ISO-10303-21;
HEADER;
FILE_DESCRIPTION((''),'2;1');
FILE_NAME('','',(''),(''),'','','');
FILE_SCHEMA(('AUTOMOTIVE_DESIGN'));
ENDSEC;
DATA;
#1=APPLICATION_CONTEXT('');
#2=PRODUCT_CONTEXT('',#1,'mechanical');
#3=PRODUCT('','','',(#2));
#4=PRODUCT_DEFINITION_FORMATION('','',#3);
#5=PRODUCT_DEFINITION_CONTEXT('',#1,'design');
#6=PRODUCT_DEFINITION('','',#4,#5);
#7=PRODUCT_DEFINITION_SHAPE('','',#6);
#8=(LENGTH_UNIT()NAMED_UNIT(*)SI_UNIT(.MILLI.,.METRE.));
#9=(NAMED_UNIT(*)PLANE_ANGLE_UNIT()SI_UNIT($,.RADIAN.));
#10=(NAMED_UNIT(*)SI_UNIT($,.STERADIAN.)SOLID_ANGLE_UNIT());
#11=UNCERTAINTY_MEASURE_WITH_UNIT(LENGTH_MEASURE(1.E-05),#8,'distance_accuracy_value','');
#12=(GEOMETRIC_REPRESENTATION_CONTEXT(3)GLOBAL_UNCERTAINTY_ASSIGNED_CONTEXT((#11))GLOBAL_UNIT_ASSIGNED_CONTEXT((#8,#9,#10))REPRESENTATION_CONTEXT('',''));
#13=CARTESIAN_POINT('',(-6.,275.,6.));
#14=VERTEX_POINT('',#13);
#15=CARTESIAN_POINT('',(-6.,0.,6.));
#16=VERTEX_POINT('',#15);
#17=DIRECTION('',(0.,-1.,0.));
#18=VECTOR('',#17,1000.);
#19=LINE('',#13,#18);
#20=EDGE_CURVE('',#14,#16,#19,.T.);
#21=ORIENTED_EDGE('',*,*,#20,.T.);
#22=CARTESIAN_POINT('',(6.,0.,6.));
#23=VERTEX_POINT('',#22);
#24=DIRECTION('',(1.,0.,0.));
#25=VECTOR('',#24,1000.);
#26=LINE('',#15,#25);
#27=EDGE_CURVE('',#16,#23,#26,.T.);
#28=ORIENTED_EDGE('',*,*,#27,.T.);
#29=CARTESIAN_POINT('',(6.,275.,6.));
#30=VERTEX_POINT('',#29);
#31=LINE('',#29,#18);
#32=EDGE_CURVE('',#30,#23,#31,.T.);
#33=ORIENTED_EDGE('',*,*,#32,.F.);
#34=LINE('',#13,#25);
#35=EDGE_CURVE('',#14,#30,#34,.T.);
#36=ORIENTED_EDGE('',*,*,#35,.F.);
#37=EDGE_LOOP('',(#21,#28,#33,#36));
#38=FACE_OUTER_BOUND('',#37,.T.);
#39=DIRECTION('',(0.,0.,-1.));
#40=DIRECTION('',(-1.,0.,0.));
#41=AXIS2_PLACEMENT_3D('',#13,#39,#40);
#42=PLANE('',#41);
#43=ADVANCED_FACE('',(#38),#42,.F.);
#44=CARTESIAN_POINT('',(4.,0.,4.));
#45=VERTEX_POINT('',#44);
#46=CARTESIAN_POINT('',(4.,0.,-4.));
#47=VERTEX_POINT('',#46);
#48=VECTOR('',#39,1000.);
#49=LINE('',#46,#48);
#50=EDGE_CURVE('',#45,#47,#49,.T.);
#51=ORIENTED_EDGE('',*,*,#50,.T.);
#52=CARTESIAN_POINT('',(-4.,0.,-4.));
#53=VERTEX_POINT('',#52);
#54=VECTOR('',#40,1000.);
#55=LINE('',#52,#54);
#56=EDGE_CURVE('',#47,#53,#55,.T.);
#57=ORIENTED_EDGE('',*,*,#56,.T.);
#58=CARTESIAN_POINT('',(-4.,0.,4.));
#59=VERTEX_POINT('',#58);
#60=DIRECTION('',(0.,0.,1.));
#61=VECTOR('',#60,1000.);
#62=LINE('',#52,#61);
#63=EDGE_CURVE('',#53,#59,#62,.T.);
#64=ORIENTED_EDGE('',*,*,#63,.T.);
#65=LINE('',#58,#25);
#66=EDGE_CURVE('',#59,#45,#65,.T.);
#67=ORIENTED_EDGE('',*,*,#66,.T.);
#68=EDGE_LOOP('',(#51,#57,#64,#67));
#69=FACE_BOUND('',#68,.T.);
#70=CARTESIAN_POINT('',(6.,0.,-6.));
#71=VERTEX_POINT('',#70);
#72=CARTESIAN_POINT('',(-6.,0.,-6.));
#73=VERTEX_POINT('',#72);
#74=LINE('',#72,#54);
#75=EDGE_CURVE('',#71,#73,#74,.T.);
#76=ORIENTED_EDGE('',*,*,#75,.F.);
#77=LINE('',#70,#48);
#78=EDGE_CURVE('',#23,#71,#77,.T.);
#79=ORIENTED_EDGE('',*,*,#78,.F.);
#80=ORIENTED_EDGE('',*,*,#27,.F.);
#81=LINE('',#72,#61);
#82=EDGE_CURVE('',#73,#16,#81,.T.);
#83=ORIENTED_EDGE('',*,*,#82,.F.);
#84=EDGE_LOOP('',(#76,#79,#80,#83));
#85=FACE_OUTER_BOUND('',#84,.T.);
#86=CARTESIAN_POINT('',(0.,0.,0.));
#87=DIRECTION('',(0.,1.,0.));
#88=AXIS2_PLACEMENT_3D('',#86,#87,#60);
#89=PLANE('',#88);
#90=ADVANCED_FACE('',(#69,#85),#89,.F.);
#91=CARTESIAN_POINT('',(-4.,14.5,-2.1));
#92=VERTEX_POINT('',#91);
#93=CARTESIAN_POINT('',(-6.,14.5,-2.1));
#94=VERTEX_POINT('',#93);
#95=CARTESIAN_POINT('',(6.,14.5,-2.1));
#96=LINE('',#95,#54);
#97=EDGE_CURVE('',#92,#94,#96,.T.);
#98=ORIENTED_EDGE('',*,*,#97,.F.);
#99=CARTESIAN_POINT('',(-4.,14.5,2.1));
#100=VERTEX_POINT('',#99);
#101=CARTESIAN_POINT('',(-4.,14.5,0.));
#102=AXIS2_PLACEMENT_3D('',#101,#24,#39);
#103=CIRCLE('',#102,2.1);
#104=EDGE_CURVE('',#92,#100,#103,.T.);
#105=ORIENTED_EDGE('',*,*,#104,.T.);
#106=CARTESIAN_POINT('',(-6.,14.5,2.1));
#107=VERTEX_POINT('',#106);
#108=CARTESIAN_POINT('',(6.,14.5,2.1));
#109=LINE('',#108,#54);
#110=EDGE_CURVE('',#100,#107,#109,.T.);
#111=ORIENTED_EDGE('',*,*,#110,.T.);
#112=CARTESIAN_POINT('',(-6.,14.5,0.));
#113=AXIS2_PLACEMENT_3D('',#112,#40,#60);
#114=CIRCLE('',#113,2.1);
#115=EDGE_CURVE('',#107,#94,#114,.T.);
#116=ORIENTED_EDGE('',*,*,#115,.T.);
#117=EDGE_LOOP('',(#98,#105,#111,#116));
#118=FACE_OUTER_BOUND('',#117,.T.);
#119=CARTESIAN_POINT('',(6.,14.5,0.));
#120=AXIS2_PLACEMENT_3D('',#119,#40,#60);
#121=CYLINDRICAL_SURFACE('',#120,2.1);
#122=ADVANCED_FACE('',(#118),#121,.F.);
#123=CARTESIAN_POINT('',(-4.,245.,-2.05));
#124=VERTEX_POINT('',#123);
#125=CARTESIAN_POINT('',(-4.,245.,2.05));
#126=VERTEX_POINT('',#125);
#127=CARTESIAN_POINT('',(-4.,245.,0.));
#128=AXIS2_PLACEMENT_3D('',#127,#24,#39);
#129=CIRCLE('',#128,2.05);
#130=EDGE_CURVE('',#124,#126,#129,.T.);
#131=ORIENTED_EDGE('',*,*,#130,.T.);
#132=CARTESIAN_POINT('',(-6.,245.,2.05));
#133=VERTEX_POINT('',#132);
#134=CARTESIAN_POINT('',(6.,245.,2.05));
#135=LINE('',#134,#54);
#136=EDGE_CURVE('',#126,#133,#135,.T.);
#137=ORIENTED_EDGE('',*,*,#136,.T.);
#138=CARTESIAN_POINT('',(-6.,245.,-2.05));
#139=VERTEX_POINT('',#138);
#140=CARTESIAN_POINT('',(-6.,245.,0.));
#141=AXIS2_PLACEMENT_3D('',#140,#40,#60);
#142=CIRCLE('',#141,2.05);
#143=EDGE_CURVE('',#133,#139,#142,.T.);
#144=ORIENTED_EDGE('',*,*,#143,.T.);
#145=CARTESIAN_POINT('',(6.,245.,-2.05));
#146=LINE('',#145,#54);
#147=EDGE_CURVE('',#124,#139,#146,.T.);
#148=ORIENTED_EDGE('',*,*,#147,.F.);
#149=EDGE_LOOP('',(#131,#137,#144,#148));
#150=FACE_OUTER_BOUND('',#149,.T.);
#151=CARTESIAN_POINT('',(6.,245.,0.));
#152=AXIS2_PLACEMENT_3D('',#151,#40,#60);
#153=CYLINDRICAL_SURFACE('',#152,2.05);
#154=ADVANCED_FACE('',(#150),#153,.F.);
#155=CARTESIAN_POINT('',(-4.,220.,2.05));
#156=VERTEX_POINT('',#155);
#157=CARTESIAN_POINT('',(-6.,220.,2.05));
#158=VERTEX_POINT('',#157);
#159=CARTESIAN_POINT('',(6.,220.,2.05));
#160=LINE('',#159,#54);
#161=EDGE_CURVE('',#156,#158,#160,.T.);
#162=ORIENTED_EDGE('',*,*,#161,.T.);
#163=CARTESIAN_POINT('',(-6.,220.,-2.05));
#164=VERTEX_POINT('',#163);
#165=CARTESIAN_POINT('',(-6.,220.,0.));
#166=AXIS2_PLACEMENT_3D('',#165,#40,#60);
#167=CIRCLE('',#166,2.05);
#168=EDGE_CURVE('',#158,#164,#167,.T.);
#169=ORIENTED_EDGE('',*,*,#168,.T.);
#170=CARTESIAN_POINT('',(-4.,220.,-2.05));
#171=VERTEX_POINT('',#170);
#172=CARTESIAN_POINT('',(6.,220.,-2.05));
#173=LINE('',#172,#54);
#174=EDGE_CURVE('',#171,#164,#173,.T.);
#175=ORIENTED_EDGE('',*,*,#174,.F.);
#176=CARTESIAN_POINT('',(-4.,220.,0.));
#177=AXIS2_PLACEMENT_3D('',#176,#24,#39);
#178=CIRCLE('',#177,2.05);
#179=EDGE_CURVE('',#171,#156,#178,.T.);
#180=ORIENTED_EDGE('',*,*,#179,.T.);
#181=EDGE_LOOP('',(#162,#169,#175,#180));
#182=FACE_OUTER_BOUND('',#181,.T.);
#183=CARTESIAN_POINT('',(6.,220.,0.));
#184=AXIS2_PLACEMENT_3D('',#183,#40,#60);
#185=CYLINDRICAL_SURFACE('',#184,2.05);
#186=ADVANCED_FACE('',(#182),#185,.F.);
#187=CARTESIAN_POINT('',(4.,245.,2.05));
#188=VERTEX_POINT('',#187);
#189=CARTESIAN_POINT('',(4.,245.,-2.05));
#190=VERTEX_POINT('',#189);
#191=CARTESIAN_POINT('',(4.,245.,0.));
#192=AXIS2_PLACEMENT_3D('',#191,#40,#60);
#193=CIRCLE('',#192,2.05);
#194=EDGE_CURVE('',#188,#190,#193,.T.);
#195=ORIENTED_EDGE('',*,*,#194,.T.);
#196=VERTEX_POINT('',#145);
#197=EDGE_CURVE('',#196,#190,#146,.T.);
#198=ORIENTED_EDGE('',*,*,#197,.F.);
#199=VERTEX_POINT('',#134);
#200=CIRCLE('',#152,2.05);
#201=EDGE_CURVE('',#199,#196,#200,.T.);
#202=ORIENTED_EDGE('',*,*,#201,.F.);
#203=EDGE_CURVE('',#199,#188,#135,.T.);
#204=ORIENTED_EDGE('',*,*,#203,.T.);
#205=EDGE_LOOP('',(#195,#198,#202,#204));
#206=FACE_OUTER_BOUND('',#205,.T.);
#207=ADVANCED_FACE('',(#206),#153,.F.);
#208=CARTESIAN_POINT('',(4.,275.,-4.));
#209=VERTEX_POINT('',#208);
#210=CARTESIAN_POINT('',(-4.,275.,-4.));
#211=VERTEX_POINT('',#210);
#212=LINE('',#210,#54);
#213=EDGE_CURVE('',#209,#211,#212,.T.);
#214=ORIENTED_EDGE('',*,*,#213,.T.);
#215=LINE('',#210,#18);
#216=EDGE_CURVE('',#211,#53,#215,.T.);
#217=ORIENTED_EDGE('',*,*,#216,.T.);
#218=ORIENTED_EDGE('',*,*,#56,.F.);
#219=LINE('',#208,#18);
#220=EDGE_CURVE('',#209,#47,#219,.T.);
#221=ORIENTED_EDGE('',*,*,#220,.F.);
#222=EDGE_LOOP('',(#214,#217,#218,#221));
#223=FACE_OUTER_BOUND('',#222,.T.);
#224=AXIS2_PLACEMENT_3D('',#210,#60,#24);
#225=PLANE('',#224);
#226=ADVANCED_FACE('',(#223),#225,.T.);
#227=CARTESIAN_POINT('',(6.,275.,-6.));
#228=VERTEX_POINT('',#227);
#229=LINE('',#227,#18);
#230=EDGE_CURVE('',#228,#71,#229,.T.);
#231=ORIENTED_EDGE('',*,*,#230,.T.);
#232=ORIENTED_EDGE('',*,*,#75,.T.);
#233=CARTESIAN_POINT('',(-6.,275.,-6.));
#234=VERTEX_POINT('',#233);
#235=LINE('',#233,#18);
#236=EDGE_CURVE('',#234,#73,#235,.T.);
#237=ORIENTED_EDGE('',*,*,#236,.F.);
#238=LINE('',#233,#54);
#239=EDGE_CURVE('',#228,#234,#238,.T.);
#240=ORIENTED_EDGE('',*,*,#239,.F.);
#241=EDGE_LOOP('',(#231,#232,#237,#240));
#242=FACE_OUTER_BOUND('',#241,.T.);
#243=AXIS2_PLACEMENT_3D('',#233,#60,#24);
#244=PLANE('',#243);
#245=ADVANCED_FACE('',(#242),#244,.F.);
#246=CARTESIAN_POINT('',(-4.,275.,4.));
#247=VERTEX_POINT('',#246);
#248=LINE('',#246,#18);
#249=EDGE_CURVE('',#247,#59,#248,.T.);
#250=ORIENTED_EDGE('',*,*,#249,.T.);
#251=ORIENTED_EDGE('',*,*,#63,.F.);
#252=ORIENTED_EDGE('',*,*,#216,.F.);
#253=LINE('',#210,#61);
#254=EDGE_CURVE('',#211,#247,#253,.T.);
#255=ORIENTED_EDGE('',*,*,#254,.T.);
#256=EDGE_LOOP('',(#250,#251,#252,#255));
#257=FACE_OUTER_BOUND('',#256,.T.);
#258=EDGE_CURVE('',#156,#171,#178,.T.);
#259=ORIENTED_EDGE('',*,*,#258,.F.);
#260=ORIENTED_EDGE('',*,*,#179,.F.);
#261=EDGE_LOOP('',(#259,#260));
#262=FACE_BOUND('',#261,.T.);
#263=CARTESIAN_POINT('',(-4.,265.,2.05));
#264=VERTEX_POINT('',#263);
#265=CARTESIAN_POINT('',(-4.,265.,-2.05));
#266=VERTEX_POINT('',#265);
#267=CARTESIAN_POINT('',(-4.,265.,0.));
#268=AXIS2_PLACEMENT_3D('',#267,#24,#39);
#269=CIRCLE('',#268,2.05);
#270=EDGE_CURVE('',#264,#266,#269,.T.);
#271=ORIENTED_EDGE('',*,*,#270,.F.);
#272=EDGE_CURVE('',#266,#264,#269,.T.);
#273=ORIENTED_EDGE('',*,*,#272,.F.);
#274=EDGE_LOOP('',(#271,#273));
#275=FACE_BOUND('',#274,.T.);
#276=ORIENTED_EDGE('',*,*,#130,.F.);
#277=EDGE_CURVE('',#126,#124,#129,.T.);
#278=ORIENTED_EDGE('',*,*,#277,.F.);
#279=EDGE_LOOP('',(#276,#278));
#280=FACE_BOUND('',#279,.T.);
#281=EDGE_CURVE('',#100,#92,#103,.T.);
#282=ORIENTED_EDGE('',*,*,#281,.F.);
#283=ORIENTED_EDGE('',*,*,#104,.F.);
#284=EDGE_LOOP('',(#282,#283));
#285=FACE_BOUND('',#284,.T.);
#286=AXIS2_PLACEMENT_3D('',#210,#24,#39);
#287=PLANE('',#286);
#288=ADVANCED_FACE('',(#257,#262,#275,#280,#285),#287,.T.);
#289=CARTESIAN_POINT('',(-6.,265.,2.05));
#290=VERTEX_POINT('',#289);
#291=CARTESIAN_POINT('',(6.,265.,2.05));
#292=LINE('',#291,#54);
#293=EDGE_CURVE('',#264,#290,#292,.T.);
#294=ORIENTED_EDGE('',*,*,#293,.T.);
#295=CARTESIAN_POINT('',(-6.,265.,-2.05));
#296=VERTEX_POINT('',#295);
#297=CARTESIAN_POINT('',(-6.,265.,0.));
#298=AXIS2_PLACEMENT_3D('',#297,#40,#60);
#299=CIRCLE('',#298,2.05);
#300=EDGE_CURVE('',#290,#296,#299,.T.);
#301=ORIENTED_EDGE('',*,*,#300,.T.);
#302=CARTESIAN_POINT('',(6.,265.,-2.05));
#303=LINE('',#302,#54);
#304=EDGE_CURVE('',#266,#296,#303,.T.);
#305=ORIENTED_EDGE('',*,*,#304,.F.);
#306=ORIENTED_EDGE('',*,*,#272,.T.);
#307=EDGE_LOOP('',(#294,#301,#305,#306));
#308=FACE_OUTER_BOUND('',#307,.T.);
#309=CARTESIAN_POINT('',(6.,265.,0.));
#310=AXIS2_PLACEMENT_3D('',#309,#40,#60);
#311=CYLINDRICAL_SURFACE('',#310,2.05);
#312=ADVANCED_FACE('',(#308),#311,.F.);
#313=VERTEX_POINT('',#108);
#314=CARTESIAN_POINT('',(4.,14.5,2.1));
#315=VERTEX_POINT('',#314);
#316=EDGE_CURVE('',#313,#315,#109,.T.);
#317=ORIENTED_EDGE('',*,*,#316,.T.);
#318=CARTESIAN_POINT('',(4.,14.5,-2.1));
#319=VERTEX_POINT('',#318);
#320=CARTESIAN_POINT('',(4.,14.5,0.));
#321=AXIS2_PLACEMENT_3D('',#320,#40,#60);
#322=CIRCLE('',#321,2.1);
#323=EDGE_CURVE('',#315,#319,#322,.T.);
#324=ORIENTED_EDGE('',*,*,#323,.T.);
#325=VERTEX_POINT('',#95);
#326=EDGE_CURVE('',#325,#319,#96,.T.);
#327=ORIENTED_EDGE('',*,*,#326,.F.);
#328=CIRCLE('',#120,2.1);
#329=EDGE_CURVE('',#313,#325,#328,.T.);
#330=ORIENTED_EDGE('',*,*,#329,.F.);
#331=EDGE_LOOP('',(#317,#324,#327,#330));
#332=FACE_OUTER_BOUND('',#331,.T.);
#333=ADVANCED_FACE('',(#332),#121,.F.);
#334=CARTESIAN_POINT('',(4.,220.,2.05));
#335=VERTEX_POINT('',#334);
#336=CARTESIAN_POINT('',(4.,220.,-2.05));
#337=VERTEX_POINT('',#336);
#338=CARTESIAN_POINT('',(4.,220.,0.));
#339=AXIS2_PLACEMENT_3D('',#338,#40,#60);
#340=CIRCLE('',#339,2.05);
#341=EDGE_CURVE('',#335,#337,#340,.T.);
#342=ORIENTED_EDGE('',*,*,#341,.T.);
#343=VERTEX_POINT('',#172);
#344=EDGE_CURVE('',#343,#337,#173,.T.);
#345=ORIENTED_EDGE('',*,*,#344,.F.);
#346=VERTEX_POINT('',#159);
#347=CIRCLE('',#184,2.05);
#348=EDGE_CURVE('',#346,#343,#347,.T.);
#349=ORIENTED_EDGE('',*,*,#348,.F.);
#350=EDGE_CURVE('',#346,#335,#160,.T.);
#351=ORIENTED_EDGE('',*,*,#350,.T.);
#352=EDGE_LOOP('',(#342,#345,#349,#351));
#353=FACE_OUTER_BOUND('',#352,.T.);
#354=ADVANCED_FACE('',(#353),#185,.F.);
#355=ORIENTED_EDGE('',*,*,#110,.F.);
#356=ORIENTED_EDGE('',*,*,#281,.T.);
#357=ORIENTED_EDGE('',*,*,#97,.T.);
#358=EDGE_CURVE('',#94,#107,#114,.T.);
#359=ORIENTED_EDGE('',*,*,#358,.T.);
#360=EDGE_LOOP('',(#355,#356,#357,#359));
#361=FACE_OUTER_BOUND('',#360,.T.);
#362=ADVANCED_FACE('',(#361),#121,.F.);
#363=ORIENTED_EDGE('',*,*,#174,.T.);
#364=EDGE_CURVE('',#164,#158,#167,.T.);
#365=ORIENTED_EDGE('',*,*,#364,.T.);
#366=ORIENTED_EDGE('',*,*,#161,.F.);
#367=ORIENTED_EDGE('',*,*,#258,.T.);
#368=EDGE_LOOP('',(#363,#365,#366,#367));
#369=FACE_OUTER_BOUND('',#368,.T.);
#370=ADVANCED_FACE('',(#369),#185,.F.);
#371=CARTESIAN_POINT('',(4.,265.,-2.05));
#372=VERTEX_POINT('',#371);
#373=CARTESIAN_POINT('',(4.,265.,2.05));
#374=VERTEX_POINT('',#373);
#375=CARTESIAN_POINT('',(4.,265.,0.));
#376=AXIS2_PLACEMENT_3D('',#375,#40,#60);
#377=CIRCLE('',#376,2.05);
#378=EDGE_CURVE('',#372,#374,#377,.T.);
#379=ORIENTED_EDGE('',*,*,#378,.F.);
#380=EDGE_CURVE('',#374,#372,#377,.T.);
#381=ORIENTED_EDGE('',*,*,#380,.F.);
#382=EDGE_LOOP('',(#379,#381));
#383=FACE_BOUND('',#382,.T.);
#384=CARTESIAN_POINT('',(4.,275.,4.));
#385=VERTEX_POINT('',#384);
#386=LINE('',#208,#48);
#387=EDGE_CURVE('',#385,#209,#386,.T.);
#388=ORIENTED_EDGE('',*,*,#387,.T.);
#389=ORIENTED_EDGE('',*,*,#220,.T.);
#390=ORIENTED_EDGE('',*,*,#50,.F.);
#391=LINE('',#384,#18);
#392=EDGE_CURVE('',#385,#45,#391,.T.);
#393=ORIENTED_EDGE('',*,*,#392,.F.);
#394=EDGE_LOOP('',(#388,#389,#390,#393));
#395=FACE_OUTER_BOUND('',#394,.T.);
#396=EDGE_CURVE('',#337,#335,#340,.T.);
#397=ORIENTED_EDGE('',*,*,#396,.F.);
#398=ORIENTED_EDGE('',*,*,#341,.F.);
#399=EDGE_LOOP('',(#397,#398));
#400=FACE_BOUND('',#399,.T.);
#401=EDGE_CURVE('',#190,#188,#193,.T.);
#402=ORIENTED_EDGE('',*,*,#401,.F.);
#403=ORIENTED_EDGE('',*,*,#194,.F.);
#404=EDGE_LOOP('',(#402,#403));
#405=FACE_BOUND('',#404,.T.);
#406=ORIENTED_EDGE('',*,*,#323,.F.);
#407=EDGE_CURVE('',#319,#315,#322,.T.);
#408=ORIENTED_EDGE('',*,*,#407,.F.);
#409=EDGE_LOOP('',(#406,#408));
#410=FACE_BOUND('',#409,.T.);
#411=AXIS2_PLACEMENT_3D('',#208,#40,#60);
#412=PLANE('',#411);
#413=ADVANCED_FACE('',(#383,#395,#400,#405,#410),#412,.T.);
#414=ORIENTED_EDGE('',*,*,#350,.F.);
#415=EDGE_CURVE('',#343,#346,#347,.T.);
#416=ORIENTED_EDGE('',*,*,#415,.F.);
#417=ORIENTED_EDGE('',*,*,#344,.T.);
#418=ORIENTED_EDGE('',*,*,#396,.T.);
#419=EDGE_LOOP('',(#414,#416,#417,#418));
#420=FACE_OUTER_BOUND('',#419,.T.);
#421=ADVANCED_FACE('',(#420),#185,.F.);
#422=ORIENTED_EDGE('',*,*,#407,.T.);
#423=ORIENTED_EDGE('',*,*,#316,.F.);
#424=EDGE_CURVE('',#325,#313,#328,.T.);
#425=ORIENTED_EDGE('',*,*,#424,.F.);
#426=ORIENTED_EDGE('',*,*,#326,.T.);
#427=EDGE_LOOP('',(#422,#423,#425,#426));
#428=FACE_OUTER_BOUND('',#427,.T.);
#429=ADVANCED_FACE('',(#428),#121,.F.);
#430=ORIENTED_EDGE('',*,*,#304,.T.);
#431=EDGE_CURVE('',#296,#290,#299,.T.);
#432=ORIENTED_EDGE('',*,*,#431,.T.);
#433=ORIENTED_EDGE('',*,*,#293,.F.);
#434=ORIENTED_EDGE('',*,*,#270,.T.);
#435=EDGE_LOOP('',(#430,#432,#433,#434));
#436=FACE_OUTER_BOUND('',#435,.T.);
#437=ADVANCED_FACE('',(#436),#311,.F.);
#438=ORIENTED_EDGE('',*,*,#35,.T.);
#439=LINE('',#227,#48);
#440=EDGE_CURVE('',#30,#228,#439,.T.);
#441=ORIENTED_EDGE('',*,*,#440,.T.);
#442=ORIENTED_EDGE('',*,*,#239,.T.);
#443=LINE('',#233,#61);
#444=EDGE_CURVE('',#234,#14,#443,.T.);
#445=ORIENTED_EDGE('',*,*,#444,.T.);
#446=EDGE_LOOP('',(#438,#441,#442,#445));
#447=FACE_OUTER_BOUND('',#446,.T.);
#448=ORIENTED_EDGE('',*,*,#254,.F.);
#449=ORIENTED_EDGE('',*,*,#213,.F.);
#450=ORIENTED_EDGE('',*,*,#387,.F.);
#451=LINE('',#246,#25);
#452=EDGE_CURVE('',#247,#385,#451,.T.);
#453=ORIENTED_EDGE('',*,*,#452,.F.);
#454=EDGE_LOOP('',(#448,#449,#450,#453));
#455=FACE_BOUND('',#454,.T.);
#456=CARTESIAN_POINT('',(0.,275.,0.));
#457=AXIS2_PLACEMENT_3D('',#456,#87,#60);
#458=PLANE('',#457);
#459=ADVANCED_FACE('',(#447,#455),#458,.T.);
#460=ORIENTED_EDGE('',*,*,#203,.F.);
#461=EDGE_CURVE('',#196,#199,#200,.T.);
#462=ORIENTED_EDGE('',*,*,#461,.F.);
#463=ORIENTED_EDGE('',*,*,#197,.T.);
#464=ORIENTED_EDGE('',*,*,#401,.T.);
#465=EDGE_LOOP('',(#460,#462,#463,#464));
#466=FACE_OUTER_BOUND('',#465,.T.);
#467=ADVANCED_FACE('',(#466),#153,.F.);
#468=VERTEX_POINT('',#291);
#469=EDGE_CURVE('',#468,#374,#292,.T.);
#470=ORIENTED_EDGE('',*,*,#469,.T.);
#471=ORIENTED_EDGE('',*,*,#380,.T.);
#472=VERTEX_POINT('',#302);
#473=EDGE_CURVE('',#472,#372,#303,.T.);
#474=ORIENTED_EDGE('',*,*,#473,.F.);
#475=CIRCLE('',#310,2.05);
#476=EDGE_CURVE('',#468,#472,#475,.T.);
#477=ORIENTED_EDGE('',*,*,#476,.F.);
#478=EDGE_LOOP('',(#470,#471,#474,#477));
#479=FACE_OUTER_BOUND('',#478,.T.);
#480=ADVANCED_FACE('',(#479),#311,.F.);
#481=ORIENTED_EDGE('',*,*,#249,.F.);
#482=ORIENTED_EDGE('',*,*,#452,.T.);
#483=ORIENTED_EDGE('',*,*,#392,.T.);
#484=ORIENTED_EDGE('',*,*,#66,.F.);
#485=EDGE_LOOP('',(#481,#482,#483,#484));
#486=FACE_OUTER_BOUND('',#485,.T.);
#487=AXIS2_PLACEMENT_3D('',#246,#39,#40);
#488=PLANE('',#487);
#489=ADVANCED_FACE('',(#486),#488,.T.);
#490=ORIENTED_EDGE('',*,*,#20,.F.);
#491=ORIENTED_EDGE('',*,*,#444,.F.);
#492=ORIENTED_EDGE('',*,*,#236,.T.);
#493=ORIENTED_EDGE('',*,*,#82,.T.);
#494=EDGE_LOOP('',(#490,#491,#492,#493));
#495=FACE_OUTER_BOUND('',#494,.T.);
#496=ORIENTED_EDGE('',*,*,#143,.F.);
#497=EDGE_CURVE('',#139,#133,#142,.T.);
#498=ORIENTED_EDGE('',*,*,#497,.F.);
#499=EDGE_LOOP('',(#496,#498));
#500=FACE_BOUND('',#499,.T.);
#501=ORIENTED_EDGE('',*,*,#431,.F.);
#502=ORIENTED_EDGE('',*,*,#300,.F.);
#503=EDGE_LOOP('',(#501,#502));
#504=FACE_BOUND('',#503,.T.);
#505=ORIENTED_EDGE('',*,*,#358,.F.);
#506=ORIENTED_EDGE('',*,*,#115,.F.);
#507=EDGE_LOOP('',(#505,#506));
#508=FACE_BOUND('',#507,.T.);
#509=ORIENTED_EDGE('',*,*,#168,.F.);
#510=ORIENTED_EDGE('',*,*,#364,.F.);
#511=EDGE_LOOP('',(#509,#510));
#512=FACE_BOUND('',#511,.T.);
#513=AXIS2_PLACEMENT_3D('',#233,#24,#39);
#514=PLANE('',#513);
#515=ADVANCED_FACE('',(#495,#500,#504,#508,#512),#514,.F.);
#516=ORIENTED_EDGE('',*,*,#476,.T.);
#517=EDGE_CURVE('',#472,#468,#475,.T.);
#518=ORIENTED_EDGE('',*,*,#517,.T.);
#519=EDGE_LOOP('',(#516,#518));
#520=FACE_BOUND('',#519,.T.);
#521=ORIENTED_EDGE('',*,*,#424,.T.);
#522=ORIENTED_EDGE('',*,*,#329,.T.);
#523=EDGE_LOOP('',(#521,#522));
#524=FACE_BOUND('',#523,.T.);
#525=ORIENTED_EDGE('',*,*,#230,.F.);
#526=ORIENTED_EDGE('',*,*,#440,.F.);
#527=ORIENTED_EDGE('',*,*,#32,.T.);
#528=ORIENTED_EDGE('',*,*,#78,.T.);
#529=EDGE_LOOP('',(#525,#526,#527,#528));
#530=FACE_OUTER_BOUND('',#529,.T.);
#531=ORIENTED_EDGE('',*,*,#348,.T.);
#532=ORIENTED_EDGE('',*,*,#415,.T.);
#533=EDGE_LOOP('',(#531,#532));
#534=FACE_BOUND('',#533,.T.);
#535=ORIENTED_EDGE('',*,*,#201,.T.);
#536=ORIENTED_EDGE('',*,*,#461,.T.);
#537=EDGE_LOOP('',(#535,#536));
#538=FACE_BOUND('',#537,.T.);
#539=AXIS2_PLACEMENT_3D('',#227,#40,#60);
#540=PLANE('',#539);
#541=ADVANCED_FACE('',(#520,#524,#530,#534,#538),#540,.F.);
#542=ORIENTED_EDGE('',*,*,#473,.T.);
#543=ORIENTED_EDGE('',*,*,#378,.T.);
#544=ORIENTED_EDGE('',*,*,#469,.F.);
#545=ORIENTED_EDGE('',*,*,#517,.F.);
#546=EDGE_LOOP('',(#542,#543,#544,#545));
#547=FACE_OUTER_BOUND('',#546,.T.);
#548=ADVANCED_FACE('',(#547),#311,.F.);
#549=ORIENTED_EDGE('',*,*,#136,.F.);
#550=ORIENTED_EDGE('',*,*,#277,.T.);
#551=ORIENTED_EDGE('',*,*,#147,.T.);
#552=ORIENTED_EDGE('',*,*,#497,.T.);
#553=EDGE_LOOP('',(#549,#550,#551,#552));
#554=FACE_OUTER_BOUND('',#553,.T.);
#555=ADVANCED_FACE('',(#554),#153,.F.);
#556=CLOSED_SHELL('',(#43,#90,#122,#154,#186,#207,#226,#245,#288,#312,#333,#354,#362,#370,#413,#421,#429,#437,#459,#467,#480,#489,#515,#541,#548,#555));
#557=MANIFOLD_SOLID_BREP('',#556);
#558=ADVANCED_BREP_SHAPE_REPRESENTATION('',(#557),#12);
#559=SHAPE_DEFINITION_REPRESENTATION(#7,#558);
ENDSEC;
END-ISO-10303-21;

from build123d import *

# Parameters (mm, degrees)
SKETCH_1_W          = 12
SKETCH_1_H          = 12
SKETCH_1_W_2        = 8
SKETCH_1_H_2        = 8
EXTRUDE_1_DEPTH     = 275
SKETCH_3_R          = 2.05
SKETCH_3_R_2        = 2.1
CUT_EXTRUDE_2_DEPTH = 276.327078218


with BuildPart() as part:
    # 草图1 → 凸台-拉伸1 (new body)
    with BuildSketch(Plane(origin=(0, 0, 0), x_dir=(1, 0, 0), z_dir=(0, 1, 0))):
        Rectangle(SKETCH_1_W, SKETCH_1_H)
        Rectangle(SKETCH_1_W_2, SKETCH_1_H_2, mode=Mode.SUBTRACT)
    extrude(amount=EXTRUDE_1_DEPTH)

    # 草图3 → 切除-拉伸2 (cut, through all)
    with BuildSketch(Plane.ZY.offset(6)):
        with Locations((0, 265)):
            Circle(SKETCH_3_R)
        with Locations((0, 245)):
            Circle(SKETCH_3_R)
        with Locations((0, 220)):
            Circle(SKETCH_3_R)
        with Locations((0, 14.5)):
            Circle(SKETCH_3_R_2)
    extrude(amount=-CUT_EXTRUDE_2_DEPTH, mode=Mode.SUBTRACT)


solid = part.part
